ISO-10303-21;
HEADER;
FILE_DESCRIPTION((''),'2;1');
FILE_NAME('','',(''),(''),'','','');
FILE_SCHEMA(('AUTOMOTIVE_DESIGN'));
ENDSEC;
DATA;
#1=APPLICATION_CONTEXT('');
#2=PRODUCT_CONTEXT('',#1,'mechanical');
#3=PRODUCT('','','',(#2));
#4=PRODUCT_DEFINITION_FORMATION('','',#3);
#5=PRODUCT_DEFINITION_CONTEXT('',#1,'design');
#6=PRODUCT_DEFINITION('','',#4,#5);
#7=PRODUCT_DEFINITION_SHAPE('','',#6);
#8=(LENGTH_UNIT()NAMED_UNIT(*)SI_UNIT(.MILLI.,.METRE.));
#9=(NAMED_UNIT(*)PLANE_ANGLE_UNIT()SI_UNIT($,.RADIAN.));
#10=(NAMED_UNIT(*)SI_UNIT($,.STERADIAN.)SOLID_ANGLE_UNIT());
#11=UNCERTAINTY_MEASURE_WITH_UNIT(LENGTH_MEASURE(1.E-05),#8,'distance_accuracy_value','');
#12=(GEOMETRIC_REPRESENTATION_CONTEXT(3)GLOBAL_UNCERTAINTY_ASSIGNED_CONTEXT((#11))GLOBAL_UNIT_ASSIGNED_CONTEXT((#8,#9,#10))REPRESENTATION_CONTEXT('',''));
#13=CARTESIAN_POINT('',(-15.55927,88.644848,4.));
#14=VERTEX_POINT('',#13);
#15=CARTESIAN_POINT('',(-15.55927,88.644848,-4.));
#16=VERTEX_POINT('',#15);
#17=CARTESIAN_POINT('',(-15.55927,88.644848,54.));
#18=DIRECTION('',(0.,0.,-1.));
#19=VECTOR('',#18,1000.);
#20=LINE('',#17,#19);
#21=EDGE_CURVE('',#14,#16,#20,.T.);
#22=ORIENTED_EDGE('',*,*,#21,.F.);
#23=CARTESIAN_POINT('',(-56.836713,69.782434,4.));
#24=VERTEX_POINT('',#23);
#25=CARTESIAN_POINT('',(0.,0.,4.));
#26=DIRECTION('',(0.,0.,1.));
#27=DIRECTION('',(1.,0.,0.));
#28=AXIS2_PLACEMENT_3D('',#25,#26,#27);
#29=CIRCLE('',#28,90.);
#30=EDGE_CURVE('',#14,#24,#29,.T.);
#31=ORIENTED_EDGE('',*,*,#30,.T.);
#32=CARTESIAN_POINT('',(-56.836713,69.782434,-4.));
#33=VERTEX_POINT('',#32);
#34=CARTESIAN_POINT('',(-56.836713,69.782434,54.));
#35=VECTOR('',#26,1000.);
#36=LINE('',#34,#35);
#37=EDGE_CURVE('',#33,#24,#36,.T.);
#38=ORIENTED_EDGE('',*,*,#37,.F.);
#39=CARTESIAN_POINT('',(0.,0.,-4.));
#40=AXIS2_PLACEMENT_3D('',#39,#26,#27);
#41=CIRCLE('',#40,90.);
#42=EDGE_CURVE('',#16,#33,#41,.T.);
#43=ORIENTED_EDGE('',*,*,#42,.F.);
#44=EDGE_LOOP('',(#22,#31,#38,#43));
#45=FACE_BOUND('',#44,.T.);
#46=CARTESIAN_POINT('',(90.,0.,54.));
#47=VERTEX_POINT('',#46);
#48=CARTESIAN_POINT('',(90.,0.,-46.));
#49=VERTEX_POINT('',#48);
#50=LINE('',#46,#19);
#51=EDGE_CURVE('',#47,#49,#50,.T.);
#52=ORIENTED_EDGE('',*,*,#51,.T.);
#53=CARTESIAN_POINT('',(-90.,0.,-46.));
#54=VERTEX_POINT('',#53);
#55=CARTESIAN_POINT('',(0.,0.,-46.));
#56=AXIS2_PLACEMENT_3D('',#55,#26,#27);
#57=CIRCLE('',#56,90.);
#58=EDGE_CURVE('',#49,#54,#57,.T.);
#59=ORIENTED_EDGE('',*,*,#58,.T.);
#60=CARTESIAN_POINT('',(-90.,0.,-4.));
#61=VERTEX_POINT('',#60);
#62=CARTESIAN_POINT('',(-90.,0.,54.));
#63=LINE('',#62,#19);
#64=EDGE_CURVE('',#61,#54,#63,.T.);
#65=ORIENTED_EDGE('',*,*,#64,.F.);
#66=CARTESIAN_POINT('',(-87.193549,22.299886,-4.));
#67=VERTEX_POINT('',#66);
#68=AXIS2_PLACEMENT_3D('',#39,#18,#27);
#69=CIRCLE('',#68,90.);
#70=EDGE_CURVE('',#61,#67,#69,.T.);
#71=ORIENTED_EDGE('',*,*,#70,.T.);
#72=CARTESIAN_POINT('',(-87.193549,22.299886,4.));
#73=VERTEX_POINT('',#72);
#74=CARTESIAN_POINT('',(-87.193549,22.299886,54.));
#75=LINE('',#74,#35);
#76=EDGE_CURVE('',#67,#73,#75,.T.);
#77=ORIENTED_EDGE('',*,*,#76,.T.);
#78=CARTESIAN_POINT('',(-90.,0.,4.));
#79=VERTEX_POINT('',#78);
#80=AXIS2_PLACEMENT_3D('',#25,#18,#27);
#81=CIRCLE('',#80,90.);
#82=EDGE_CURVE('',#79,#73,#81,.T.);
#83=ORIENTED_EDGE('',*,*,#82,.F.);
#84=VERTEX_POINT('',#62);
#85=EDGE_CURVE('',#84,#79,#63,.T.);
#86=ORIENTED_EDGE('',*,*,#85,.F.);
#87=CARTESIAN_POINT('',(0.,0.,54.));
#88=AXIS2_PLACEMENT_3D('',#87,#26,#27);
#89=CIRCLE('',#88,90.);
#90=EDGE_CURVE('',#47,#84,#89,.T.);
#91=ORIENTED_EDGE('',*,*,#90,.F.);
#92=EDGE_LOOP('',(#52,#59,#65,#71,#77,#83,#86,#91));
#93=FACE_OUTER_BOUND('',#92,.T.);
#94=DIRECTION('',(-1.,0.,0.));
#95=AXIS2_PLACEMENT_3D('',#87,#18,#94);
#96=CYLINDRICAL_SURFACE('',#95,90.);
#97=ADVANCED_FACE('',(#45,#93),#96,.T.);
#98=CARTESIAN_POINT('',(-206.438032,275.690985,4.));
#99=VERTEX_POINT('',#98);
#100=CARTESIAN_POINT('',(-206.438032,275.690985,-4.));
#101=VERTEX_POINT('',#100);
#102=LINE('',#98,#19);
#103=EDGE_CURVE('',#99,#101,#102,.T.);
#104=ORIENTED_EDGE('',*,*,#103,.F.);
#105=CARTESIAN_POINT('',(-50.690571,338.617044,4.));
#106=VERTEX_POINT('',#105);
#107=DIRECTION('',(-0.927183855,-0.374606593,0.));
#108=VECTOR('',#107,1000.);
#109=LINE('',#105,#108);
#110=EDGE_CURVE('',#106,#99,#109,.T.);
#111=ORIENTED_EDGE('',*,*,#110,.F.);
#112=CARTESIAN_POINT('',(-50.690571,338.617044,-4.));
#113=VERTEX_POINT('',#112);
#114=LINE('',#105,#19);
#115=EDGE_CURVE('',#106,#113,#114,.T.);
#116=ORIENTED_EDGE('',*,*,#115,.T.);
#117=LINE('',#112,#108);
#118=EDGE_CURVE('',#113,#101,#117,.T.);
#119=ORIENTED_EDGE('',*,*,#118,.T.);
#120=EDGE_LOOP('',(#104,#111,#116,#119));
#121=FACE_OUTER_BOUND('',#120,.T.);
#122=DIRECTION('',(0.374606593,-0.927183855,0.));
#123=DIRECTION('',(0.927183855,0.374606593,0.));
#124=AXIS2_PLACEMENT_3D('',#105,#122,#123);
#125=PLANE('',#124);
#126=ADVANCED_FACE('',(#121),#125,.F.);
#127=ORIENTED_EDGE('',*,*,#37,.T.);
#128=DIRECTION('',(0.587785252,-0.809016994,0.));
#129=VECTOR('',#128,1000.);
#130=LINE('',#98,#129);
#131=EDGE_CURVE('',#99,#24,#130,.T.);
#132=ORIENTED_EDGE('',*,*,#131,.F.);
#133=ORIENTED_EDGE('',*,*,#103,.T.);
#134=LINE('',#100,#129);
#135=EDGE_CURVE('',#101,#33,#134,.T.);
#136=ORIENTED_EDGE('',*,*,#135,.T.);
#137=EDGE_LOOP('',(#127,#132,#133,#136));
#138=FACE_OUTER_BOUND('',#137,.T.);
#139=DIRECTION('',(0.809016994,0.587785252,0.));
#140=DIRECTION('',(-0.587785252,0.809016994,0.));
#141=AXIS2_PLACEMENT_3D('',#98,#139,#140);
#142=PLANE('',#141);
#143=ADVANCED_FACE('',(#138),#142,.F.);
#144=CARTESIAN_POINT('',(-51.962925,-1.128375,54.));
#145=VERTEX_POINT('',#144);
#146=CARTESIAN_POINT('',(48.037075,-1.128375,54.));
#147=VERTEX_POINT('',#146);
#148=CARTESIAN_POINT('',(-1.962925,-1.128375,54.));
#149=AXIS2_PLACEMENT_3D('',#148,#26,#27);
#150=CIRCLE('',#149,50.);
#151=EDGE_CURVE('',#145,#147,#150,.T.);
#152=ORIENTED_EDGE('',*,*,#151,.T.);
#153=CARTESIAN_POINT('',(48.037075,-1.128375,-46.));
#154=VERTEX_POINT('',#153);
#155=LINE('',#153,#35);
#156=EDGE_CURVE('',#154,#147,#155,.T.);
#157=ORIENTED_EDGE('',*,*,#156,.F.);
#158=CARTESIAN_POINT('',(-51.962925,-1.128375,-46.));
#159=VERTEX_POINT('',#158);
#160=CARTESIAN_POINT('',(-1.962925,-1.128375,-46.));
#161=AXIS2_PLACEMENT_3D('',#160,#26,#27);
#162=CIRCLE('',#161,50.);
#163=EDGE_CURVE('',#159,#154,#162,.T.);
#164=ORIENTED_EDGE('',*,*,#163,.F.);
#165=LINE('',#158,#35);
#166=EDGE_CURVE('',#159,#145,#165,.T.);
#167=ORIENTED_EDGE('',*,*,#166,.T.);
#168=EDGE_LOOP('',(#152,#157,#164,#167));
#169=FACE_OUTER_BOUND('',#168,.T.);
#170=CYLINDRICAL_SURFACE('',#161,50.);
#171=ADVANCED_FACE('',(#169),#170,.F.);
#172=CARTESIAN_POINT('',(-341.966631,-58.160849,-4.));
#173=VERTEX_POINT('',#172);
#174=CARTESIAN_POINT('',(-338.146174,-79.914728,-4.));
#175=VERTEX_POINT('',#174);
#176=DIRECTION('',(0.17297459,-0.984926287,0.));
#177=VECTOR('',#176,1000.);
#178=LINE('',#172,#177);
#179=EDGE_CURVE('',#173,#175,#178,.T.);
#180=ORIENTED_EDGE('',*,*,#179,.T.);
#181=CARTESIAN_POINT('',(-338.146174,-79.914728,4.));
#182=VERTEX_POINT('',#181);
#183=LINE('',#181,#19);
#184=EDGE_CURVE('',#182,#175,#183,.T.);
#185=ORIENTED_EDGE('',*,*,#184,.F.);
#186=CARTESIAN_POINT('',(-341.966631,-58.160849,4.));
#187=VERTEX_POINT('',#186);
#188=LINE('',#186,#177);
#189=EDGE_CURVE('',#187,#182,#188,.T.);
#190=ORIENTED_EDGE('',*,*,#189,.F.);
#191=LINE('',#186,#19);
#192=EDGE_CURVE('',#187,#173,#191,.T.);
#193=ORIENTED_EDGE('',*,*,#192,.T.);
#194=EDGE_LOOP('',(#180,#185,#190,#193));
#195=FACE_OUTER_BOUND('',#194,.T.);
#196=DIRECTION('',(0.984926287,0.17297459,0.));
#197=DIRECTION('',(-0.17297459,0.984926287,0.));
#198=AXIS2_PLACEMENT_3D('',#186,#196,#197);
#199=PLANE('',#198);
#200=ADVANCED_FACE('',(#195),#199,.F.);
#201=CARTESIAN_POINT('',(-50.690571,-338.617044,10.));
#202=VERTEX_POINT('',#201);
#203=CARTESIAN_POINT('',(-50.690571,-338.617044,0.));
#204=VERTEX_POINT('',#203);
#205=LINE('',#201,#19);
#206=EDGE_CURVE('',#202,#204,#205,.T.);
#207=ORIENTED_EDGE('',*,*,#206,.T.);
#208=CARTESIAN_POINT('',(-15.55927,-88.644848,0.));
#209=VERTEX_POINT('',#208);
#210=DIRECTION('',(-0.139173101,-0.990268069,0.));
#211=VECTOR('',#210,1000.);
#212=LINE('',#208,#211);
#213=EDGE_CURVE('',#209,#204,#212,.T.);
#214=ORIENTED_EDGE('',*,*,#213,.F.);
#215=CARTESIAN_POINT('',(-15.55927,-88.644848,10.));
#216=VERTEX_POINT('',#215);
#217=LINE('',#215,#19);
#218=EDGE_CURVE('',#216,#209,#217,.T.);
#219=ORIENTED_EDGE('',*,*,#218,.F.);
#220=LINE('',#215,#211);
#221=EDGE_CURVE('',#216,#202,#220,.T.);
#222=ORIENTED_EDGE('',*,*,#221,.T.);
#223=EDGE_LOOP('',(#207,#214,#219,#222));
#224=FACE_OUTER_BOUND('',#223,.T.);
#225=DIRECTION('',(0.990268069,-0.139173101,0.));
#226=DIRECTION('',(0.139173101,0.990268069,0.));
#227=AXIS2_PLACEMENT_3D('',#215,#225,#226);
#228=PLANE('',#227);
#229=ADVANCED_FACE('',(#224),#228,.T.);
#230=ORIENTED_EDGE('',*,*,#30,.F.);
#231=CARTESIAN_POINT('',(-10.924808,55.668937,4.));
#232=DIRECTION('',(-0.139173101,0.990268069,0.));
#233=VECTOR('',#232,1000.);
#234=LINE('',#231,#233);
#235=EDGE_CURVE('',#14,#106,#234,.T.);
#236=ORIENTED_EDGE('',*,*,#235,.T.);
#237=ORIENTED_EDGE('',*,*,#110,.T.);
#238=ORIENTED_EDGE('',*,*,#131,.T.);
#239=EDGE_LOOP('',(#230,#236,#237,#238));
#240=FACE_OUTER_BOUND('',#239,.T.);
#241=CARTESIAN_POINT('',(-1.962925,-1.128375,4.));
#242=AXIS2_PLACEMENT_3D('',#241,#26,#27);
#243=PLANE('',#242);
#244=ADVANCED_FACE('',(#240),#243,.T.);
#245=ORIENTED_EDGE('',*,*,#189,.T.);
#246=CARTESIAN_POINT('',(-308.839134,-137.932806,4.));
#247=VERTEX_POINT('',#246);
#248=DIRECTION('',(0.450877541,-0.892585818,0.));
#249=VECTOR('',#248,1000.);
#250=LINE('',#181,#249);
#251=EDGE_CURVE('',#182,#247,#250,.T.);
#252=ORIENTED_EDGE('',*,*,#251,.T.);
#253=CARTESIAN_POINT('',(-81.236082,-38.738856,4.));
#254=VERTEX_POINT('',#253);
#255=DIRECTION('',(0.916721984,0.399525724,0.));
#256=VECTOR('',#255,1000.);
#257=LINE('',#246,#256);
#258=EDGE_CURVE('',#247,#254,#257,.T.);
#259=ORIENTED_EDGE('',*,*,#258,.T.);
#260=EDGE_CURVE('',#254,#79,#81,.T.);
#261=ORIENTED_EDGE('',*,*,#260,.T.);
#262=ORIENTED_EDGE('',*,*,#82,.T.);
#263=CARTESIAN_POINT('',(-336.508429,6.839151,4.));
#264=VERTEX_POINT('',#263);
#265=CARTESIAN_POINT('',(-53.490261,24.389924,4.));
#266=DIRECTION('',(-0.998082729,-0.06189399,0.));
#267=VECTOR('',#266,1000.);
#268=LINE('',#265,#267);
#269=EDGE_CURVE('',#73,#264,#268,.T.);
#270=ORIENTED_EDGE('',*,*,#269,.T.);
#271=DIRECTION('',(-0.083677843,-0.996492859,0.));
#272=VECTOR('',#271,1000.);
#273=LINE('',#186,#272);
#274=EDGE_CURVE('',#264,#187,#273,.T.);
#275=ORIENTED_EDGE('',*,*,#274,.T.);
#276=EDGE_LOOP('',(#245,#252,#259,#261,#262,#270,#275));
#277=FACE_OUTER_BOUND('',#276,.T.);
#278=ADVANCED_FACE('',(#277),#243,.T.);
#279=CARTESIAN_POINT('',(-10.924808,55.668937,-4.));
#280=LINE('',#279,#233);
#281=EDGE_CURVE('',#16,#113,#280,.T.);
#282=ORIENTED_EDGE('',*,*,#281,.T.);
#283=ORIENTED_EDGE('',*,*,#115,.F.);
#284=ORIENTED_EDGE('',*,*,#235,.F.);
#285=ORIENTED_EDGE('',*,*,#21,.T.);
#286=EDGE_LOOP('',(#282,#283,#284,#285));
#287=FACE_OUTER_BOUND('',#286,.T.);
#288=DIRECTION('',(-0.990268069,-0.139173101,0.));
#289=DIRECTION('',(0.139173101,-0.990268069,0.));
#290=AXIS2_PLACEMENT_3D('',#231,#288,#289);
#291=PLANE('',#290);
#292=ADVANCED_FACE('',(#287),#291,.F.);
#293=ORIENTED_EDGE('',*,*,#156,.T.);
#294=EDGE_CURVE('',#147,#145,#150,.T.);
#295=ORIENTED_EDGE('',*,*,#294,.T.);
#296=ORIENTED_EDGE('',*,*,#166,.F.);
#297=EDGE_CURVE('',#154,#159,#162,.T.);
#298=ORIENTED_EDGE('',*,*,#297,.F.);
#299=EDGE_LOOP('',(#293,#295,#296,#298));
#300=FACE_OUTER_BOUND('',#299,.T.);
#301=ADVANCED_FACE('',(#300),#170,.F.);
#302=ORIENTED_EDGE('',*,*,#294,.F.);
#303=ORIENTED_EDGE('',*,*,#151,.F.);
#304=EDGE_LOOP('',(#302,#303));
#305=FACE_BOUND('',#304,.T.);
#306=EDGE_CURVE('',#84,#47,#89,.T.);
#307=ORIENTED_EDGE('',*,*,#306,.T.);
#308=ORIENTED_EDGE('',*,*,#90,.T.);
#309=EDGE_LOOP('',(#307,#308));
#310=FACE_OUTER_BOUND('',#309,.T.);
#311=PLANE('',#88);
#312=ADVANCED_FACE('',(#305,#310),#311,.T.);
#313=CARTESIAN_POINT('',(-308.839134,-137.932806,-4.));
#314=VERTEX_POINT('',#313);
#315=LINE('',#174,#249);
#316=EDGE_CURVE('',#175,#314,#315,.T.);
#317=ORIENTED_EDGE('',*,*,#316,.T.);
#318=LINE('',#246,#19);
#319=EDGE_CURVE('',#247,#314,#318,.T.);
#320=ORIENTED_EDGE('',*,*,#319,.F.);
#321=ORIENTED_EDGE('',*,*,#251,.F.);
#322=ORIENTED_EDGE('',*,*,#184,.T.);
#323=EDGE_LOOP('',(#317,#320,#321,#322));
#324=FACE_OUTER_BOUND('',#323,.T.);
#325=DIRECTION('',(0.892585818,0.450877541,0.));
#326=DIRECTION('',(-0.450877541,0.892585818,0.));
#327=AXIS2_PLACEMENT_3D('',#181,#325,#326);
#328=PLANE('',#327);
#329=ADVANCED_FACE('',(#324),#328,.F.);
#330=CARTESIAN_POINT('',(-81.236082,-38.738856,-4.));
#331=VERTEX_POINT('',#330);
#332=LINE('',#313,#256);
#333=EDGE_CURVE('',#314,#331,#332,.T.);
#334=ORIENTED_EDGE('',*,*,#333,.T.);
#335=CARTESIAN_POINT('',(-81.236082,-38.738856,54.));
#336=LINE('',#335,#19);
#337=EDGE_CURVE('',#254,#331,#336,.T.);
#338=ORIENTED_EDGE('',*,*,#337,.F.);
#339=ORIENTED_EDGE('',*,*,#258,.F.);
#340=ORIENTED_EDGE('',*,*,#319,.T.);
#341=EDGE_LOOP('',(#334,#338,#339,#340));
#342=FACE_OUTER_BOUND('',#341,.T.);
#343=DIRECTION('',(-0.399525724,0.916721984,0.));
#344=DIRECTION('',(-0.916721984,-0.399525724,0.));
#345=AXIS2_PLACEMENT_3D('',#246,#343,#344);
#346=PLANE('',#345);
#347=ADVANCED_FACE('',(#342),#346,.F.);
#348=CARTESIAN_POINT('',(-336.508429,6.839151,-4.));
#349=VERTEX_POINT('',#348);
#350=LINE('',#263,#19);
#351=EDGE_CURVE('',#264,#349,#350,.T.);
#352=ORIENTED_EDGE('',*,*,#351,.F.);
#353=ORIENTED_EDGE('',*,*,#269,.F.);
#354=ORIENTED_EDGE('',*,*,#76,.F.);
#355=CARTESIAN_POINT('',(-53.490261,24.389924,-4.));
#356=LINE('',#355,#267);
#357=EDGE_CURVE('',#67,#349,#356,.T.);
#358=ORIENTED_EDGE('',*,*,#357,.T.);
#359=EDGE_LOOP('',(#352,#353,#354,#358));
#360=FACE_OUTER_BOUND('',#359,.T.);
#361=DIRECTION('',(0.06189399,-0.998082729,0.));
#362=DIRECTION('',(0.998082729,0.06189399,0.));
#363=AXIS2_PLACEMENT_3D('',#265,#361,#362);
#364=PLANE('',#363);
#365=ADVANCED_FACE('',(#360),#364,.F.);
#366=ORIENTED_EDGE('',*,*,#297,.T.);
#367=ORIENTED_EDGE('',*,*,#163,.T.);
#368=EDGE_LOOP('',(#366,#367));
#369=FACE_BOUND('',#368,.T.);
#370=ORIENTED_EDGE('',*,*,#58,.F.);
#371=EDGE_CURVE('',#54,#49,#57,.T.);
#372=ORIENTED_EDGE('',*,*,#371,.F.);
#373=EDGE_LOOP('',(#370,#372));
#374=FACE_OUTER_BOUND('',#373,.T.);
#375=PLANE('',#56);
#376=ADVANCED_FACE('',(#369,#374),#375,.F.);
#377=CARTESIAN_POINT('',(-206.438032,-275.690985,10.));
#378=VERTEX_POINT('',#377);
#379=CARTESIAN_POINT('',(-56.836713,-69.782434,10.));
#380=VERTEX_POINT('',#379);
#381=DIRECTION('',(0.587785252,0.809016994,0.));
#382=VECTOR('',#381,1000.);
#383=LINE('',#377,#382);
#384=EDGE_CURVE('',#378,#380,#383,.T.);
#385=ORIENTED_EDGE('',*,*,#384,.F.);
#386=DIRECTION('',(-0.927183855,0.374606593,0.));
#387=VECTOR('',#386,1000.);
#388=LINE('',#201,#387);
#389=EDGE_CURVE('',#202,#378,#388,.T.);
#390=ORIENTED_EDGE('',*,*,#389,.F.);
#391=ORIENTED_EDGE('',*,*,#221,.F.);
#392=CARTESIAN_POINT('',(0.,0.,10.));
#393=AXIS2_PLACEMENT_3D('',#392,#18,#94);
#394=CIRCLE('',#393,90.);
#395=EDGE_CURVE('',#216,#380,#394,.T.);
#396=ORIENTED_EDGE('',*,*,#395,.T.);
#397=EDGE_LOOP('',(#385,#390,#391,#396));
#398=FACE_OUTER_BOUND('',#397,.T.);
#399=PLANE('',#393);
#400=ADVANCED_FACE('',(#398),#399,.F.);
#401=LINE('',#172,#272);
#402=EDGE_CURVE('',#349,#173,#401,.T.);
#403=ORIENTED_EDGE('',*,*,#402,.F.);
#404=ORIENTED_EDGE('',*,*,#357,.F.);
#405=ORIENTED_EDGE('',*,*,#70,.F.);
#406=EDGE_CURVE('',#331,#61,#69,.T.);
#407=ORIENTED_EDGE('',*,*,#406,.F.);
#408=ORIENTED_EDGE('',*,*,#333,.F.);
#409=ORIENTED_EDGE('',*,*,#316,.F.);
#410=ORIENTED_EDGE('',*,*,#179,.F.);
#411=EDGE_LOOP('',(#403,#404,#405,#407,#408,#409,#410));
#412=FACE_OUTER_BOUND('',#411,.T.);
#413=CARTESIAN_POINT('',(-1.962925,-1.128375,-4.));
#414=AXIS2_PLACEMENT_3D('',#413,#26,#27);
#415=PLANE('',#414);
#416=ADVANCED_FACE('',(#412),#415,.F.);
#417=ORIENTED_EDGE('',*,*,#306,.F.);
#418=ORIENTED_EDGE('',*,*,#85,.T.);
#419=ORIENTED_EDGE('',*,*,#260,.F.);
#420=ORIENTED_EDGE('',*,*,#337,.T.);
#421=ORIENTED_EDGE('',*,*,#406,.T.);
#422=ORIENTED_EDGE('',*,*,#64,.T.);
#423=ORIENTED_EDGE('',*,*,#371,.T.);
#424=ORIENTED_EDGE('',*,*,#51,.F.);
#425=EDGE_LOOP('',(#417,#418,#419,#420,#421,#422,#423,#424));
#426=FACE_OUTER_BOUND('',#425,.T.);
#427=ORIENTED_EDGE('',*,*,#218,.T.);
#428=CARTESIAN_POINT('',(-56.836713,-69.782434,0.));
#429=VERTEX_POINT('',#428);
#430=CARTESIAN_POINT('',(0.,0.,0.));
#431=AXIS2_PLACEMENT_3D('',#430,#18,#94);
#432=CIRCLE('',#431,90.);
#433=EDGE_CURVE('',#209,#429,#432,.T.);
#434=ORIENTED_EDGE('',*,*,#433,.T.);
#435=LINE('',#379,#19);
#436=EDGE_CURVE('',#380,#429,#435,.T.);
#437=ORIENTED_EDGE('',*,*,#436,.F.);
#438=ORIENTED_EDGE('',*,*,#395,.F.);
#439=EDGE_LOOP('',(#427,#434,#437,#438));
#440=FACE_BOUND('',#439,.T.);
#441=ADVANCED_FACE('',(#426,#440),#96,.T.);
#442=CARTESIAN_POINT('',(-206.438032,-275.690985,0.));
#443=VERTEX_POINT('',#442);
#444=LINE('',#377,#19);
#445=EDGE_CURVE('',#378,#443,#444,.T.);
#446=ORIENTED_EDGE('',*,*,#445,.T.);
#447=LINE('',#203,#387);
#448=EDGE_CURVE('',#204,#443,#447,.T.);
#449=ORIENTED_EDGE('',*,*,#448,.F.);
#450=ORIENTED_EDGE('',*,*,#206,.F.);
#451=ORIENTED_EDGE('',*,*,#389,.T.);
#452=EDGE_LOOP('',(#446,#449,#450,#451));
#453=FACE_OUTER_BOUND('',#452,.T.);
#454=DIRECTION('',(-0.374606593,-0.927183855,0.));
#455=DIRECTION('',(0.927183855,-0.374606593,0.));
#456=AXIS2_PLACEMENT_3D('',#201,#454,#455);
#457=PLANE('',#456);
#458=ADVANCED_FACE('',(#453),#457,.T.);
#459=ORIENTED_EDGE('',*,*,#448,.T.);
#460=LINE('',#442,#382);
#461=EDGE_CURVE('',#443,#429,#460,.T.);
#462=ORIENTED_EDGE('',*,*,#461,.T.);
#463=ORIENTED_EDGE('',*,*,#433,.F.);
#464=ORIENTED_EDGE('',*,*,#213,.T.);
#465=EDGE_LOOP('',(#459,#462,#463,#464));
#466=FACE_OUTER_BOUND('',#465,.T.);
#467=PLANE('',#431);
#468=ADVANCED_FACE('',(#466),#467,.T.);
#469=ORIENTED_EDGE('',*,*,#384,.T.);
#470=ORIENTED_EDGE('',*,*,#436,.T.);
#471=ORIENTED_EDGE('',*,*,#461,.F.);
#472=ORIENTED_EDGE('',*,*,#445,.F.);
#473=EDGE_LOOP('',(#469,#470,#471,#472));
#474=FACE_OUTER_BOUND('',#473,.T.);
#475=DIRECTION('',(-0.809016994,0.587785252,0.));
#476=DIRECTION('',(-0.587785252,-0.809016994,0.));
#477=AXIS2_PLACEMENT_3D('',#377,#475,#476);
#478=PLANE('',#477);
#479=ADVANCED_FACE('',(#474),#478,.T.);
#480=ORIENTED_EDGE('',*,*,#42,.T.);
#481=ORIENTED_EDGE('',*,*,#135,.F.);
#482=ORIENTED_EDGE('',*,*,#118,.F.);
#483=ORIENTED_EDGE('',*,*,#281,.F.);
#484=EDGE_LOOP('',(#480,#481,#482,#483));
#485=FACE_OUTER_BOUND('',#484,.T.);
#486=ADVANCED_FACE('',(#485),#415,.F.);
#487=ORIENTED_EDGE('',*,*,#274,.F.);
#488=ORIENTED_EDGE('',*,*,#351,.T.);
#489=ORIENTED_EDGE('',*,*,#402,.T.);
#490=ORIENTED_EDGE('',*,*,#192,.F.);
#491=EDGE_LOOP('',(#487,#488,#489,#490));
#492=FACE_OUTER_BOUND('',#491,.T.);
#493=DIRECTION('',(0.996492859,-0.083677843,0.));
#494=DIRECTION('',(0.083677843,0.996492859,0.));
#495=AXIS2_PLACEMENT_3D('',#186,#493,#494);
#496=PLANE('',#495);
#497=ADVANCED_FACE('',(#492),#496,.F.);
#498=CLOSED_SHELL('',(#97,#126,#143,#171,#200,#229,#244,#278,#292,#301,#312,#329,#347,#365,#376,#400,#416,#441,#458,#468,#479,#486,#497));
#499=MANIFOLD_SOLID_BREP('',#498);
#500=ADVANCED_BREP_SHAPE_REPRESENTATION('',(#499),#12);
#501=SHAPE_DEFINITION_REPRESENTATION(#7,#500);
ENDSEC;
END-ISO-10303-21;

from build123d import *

# Parameters (mm, degrees)
EXTRUDE_1_DEPTH     = 4
EXTRUDE_1_2_DEPTH   = 4
EXTRUDE_1_3_DEPTH   = 4
SKETCH_2_R          = 90
SKETCH_2_R_2        = 57.5
EXTRUDE_2_DEPTH     = 50
SKETCH_4_R          = 57.5
SKETCH_4_R_2        = 50
EXTRUDE_3_DEPTH     = 100
CUT_EXTRUDE_1_DEPTH = 485.810454508
EXTRUDE_START       = 10
EXTRUDE_4_DEPTH     = 10


with BuildPart() as part:
    # 草图1 → 凸台-拉伸1 (new, symmetric)
    with BuildSketch(Plane.XY):
        with BuildLine():
            Line((-10.924807901, 55.668937127), (-50.690571005, 338.617043901))
            Line((-50.690571005, 338.617043901), (-206.438031879, 275.690985101))
            Line((-206.438031879, 275.690985101), (-37.918188894, 43.743319974))
            ThreePointArc((-37.918188894, 43.743319974), (-25.199590106, 51.467322598), (-10.924807901, 55.668937127))
        make_face()
    extrude(amount=EXTRUDE_1_DEPTH, both=True)



with BuildPart() as body_2:
    # 草图1 → Extrude 1 2 (new, symmetric)
    with BuildSketch(Plane.XY):
        with BuildLine():
            Line((-341.966631122, -58.160848878), (-338.146174396, -79.914727665))
            Line((-338.146174396, -79.914727665), (-308.839134252, -137.932805865))
            Line((-308.839134252, -137.932805865), (-53.490261468, -26.646674297))
            ThreePointArc((-53.490261468, -26.646674297), (-59.462925063, -1.128374922), (-53.490261468, 24.389924453))
            Line((-53.490261468, 24.389924453), (-336.508428621, 6.839151122))
            Line((-336.508428621, 6.839151122), (-341.966631122, -58.160848878))
        make_face()
    extrude(amount=EXTRUDE_1_2_DEPTH, both=True)


with BuildPart() as body_3:
    # 草图1 → Extrude 1 3 (new, symmetric)
    with BuildSketch(Plane.XY):
        with BuildLine():
            Line((-14.977351718, -57.136184189), (-46.962925063, -340))
            Line((-46.962925063, -340), (68.037074937, -340))
            Line((68.037074937, -340), (24.752563392, -52.045294277))
            ThreePointArc((24.752563392, -52.045294277), (5.345225431, -58.162057394), (-14.977351718, -57.136184189))
        make_face()
    extrude(amount=EXTRUDE_1_3_DEPTH, both=True)


with BuildPart() as part_1:
    add(part.part)

    add(body_2.part)  # 凸台-拉伸2 merges body 2

    add(body_3.part)  # 凸台-拉伸2 merges body 3
    # 草图2 → 凸台-拉伸2 (add, symmetric)
    with BuildSketch(Plane.XY.offset(4)):
        Circle(SKETCH_2_R)
        with Locations((-1.962925063, -1.128374922)):
            Circle(SKETCH_2_R_2, mode=Mode.SUBTRACT)
    extrude(amount=EXTRUDE_2_DEPTH, both=True)

    # 草图4 → 凸台-拉伸3 (add)
    with BuildSketch(Plane.XY.offset(54)):
        with Locations((-1.962925063, -1.128374922)):
            Circle(SKETCH_4_R)
        with Locations((-1.962925063, -1.128374922)):
            Circle(SKETCH_4_R_2, mode=Mode.SUBTRACT)
    extrude(amount=-EXTRUDE_3_DEPTH)

    # 草图7 → 切除-拉伸1 (cut, through all)
    with BuildSketch(Plane.XY.offset(4)):
        with BuildLine():
            Line((-18.476741558, -88.082972369), (-46.962925063, -340))
            Line((-46.962925063, -340), (68.037074937, -340))
            Line((68.037074937, -340), (29.699950595, -84.958301152))
            ThreePointArc((29.699950595, -84.958301152), (5.825032002, -89.811296629), (-18.476741558, -88.082972369))
        make_face()
    extrude(amount=-CUT_EXTRUDE_1_DEPTH, mode=Mode.SUBTRACT)

    # 草图9 → 凸台-拉伸4 (add)
    with BuildSketch(Plane.XY.offset(EXTRUDE_START)):
        with BuildLine():
            Line((-206.438031879, -275.690985101), (-56.836712635, -69.782434014))
            ThreePointArc((-56.836712635, -69.782434014), (-37.406446529, -81.858156332), (-15.559269973, -88.644848231))
            Line((-15.559269973, -88.644848231), (-50.690571005, -338.617043901))
            Line((-50.690571005, -338.617043901), (-206.438031879, -275.690985101))
        make_face()
    extrude(amount=-EXTRUDE_4_DEPTH)


solid = part_1.part
